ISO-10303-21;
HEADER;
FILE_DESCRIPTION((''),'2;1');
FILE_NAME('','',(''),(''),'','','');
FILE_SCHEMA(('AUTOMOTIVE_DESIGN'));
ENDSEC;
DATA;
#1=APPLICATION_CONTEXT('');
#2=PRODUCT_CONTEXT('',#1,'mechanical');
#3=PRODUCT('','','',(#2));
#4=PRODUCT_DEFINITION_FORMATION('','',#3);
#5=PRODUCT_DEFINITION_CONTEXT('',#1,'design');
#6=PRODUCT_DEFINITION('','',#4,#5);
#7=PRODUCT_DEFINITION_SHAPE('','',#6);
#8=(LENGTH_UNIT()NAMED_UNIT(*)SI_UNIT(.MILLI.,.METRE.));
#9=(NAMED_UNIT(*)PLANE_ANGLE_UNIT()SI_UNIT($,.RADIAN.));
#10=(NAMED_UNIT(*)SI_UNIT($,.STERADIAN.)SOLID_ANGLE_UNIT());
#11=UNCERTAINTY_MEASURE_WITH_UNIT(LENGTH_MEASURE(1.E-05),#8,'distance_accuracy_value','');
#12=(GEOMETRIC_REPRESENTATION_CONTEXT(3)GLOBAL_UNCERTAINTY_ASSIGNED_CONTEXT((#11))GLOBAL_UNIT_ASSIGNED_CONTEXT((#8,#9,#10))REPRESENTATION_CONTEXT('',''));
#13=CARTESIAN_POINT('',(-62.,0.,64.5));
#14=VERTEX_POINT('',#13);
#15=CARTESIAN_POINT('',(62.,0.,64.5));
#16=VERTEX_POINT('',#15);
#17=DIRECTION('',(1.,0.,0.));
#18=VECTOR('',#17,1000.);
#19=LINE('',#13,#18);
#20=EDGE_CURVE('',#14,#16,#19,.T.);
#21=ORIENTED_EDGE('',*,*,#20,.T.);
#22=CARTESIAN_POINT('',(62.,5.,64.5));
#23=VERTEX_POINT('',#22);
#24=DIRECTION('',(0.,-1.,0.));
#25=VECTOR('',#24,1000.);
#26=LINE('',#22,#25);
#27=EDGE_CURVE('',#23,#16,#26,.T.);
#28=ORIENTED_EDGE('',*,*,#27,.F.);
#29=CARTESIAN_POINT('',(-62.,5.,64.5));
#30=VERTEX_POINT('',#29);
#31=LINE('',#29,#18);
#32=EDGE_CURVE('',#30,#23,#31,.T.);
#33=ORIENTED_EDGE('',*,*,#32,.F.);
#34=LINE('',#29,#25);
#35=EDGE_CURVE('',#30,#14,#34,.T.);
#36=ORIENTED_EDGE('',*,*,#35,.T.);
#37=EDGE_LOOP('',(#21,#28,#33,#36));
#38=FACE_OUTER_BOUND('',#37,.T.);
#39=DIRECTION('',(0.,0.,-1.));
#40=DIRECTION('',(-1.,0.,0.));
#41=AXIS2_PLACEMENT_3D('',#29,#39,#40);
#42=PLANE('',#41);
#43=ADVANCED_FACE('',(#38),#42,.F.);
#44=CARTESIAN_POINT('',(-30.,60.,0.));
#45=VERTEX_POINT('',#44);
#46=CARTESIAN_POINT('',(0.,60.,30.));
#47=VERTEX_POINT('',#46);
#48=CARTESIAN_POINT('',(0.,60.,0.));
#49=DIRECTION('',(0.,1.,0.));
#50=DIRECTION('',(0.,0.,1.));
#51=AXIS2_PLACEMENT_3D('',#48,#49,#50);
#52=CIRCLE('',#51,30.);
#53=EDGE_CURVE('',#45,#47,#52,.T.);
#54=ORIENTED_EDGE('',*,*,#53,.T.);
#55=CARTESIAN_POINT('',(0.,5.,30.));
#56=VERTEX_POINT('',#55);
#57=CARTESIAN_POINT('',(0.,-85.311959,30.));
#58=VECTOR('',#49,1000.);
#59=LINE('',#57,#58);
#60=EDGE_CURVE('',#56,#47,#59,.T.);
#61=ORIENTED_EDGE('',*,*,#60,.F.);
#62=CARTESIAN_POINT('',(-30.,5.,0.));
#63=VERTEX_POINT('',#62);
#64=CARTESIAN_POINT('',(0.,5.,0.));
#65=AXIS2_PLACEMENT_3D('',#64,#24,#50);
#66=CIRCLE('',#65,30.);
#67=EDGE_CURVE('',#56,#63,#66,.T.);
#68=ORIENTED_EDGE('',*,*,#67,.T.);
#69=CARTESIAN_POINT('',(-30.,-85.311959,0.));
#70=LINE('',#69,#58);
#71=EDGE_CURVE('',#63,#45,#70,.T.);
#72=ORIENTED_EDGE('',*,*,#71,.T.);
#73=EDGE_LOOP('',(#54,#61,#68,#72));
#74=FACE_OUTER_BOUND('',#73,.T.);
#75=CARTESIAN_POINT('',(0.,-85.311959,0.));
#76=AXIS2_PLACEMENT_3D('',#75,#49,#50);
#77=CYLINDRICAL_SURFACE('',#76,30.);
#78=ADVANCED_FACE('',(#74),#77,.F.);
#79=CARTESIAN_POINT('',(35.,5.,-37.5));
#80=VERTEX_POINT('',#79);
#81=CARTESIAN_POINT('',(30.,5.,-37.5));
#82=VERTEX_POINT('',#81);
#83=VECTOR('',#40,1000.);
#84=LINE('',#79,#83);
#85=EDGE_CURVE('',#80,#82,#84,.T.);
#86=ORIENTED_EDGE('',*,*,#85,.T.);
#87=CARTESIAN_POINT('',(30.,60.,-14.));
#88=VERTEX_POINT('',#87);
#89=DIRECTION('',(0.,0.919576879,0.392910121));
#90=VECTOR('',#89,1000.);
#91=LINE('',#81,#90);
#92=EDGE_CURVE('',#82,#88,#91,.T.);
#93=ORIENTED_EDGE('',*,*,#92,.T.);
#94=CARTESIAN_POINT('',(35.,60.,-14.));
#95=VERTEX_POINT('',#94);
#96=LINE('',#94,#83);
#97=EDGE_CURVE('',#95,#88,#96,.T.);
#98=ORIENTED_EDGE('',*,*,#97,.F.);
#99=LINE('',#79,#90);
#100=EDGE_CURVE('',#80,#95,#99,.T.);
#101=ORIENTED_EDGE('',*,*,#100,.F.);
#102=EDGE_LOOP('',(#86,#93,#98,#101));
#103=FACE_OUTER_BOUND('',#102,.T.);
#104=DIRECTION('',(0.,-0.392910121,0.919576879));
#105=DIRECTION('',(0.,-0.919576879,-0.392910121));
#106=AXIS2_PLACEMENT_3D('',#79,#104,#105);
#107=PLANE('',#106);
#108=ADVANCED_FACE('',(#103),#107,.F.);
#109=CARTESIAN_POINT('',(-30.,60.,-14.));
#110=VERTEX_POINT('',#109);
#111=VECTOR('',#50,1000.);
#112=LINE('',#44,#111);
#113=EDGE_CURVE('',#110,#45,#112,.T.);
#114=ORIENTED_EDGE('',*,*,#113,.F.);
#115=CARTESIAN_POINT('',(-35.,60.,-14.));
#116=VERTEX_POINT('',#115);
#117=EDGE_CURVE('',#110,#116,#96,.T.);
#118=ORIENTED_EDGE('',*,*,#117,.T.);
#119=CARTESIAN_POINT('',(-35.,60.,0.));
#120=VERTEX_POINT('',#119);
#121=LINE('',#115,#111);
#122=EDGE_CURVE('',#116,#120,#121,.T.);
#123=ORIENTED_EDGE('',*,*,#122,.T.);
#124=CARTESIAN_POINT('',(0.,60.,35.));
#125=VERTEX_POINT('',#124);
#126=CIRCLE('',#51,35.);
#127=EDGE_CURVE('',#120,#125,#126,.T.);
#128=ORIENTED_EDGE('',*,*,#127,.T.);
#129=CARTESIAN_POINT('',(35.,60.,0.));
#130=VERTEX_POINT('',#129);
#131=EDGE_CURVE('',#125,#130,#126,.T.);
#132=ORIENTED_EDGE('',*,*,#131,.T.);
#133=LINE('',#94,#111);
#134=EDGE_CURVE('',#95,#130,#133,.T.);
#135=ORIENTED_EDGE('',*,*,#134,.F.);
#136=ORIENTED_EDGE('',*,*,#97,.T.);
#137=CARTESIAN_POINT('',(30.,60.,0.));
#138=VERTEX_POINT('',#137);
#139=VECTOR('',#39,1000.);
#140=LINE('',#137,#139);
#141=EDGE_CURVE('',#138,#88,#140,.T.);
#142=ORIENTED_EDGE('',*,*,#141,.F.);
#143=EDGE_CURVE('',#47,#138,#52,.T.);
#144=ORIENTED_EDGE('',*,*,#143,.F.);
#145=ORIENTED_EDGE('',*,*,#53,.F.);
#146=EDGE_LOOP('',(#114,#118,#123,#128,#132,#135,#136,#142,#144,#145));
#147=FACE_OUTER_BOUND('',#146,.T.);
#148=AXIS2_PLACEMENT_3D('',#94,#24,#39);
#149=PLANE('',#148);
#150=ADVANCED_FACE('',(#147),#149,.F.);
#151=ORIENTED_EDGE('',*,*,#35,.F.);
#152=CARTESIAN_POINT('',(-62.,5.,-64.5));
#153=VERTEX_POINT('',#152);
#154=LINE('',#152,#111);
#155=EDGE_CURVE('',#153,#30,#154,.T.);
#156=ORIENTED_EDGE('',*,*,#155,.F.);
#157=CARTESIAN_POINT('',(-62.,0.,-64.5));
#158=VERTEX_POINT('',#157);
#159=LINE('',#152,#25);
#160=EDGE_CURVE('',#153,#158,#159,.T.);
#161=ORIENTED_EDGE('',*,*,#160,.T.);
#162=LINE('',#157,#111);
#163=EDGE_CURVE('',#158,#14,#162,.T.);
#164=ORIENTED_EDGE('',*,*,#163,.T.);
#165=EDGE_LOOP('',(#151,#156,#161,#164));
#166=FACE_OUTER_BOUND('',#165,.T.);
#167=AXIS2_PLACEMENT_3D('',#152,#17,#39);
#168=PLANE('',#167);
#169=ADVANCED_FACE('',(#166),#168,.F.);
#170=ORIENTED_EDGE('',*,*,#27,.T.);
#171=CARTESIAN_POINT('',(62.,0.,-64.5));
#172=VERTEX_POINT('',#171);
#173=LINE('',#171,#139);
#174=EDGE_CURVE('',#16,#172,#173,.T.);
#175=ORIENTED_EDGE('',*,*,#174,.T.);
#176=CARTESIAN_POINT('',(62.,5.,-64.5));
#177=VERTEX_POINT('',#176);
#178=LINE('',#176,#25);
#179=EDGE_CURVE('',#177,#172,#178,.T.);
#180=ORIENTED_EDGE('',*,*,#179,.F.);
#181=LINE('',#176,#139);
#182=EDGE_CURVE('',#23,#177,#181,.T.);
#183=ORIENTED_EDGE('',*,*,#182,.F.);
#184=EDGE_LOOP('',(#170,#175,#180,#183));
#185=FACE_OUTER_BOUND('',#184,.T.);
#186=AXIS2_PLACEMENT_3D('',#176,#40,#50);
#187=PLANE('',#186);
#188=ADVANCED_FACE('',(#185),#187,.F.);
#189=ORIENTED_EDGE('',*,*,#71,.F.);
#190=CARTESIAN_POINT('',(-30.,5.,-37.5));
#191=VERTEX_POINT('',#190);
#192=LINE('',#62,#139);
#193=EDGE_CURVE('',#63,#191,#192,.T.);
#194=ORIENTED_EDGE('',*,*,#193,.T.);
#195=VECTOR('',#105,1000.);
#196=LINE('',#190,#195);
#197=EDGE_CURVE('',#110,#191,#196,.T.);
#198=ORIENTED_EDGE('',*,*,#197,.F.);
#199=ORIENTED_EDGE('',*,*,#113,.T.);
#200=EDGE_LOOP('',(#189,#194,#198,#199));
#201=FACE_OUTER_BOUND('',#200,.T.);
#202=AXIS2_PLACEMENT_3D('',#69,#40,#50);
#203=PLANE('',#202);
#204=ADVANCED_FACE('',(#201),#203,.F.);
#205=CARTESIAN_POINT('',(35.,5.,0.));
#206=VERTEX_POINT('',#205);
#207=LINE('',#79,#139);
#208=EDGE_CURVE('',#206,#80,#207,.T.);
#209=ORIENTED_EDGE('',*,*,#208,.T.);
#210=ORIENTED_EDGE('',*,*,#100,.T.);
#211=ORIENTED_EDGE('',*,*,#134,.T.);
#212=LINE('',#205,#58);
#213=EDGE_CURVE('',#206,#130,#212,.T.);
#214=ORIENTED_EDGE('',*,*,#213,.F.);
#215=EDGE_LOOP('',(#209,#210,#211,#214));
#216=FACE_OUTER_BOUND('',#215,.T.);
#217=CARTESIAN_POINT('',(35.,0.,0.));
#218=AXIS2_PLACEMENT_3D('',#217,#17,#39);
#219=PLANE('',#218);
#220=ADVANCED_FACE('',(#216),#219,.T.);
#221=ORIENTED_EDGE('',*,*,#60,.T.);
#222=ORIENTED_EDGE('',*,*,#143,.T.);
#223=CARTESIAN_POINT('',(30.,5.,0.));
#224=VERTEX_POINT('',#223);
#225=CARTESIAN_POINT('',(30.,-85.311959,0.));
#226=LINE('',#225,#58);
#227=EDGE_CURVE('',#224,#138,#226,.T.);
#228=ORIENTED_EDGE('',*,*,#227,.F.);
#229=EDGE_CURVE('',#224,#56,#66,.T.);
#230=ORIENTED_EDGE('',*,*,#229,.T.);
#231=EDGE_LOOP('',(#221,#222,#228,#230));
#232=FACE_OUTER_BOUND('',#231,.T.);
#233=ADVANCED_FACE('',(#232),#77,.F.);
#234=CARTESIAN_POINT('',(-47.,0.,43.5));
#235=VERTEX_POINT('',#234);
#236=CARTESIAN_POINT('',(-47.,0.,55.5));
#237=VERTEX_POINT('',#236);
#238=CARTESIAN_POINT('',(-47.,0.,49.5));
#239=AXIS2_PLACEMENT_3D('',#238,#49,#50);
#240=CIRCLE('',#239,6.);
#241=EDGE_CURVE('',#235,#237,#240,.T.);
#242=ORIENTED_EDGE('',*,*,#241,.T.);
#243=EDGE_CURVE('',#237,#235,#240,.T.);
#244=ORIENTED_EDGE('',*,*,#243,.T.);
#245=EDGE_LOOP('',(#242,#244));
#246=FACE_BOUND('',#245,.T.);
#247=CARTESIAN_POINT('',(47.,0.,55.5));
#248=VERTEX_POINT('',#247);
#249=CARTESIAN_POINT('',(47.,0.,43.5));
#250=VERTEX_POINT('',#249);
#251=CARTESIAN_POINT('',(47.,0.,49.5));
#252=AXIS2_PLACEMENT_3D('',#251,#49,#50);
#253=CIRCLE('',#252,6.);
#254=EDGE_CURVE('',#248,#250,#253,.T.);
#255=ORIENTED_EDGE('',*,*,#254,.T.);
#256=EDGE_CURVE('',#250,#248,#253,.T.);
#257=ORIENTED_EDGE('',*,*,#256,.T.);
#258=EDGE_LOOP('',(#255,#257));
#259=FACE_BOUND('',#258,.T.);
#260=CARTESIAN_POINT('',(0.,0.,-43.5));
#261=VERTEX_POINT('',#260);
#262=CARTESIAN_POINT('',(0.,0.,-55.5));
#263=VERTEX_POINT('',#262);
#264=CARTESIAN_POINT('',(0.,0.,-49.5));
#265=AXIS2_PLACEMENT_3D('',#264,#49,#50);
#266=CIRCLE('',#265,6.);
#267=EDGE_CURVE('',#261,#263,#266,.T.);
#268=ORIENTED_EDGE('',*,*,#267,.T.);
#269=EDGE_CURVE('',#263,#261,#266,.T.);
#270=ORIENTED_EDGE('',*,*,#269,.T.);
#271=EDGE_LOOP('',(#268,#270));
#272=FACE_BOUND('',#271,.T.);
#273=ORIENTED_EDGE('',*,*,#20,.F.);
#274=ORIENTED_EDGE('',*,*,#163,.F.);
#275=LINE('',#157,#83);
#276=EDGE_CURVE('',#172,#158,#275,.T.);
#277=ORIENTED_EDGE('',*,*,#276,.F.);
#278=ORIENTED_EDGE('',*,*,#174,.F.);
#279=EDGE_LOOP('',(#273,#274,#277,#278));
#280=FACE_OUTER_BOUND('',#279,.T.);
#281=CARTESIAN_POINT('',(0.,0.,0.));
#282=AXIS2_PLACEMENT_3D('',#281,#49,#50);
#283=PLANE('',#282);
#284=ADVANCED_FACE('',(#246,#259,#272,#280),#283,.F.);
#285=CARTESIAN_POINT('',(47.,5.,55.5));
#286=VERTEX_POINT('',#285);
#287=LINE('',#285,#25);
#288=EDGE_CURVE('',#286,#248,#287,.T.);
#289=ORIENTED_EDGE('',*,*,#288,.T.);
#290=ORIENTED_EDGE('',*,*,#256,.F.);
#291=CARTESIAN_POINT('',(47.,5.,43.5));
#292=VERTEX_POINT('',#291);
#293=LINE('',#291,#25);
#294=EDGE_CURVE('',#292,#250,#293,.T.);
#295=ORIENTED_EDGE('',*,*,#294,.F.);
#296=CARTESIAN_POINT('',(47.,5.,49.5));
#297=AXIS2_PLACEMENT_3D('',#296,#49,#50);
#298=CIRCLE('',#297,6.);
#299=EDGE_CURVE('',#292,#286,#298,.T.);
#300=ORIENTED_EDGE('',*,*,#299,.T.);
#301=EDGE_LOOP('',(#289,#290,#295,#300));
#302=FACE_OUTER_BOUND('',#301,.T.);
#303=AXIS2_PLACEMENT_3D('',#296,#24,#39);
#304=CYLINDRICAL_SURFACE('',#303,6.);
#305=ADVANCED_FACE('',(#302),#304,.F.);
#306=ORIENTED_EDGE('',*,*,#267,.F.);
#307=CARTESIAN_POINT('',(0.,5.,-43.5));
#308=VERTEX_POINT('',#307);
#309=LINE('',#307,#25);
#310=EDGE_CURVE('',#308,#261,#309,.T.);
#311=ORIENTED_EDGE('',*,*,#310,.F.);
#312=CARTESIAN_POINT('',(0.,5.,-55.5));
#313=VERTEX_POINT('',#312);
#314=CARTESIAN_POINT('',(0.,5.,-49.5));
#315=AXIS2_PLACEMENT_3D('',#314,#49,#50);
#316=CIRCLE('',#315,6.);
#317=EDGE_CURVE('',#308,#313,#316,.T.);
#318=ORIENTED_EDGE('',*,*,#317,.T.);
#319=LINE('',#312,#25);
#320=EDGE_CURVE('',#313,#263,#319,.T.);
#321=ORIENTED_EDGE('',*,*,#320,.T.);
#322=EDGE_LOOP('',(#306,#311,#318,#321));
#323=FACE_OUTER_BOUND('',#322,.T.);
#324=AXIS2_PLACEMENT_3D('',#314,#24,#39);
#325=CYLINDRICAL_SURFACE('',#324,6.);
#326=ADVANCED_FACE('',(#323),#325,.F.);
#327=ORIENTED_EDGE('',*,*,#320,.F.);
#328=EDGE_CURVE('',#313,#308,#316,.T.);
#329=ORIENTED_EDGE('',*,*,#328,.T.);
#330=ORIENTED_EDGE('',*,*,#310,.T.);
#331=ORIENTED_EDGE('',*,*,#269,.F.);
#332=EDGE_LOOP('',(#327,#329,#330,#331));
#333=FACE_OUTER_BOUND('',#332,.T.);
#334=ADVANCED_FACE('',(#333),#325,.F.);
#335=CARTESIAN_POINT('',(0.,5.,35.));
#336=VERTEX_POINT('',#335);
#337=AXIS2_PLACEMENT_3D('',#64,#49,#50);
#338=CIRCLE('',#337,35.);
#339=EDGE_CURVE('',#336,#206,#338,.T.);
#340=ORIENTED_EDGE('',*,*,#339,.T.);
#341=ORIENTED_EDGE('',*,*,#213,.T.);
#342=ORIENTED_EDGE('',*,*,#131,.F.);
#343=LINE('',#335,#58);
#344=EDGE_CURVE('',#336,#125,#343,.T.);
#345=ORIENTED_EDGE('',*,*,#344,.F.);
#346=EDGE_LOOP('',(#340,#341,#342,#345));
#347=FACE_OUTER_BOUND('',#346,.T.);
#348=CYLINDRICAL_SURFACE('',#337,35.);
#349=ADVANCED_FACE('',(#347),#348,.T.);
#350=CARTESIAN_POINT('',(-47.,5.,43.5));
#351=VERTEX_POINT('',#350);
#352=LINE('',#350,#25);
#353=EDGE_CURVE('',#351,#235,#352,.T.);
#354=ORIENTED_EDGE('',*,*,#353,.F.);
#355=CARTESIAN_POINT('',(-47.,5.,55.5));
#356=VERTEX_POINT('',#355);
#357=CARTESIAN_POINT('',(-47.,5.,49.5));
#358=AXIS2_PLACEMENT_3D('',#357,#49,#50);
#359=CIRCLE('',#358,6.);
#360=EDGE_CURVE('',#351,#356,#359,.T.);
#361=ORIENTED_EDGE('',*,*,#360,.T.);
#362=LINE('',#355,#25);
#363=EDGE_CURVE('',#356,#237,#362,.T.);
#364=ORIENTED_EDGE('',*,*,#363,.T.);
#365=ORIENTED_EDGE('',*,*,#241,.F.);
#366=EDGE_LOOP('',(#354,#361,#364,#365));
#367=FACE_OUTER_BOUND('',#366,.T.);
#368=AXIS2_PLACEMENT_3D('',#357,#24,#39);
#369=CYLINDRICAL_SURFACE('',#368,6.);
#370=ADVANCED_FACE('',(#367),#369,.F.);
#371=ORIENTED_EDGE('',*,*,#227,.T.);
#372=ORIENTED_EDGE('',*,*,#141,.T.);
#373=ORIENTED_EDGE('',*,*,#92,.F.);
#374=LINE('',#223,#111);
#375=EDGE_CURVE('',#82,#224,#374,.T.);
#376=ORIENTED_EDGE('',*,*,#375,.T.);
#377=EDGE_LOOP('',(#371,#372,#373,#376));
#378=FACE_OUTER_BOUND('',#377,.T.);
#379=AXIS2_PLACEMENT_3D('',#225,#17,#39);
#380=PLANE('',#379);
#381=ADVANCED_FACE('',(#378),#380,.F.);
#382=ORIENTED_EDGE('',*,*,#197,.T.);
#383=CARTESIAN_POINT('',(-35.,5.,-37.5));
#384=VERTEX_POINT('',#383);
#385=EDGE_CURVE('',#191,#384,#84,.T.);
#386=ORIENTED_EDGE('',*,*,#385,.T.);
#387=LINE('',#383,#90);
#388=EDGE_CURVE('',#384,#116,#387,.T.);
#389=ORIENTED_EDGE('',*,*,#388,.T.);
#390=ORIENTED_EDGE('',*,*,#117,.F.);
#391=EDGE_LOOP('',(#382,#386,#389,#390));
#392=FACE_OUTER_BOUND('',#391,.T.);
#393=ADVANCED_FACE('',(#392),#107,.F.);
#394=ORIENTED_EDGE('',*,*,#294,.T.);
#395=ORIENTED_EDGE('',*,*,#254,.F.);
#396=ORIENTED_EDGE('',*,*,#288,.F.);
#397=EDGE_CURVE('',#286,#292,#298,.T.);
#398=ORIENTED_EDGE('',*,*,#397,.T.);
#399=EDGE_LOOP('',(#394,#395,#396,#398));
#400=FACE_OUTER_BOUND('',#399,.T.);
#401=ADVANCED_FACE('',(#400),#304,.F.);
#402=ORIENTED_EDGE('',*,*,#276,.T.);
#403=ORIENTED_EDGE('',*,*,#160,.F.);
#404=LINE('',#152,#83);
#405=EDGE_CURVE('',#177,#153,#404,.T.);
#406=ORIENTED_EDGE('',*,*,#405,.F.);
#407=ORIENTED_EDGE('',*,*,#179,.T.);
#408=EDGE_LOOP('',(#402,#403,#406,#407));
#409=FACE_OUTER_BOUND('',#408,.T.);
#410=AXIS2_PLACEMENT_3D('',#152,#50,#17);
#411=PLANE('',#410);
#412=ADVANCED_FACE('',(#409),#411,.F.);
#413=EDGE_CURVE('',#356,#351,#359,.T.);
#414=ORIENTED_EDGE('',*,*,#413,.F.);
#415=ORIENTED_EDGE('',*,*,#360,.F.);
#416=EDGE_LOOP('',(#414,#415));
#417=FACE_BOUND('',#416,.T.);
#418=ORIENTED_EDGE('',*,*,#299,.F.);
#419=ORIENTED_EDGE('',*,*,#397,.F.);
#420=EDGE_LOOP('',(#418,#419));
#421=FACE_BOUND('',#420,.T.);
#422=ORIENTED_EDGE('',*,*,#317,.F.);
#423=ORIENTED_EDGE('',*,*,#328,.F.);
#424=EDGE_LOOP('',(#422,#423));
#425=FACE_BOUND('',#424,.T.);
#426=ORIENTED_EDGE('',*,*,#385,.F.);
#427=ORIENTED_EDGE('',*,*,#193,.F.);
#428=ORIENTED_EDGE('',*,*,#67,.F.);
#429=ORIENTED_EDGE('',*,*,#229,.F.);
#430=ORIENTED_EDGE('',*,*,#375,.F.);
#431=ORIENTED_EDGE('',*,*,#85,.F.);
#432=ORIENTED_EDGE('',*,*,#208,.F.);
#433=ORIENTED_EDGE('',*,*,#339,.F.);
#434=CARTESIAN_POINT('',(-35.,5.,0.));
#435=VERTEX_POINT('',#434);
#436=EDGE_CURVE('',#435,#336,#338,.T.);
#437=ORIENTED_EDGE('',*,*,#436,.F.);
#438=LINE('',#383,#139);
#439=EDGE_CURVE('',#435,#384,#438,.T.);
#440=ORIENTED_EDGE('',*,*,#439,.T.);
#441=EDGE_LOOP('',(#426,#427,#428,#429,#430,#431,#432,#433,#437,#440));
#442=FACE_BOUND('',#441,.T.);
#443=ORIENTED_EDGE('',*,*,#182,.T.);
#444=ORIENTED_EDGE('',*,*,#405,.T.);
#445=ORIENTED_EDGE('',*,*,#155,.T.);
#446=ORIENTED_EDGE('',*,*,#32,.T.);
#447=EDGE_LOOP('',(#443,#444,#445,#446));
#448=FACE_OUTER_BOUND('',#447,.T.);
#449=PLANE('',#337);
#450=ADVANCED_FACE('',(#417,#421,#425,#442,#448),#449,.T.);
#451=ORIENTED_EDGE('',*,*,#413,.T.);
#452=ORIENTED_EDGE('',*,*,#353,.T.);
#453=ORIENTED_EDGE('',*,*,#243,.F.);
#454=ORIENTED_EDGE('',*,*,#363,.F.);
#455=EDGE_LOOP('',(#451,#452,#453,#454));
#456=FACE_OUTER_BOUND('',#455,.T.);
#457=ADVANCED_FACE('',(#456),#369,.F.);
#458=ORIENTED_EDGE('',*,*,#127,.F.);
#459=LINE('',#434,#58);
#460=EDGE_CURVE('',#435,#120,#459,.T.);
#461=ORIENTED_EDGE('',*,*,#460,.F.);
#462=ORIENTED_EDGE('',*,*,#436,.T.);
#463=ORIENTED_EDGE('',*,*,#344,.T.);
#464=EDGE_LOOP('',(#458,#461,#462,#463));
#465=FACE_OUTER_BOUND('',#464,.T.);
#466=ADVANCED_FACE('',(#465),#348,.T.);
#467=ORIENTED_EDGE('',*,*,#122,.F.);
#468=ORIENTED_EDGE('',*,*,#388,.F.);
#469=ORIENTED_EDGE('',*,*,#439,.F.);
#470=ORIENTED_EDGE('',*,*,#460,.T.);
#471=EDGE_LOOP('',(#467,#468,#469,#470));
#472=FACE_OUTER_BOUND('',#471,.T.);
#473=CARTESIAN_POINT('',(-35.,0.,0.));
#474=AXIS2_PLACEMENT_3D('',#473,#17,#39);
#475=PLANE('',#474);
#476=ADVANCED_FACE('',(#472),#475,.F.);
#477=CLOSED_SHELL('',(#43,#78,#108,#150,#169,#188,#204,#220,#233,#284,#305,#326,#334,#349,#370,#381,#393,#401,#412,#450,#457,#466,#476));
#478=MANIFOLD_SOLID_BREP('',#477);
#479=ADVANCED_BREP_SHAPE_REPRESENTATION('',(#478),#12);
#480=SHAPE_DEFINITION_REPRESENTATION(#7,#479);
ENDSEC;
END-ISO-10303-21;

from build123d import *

# Parameters (mm, degrees)
BASE_PLATE_SKETCH_W         = 124
BASE_PLATE_SKETCH_H         = 129
BASE_PLATE_SKETCH_R         = 6
BASE_PLATE_DEPTH            = 5
UPRIGHT_SUPPORT_BLOCK_DEPTH = 35
CRADLE_CUT_SKETCH_W         = 60
CRADLE_CUT_SKETCH_H         = 23.5
CRADLE_CUT_DEPTH            = 55
GUSSET_TRIM_CUT_DEPTH       = 55


with BuildPart() as part:
    # Base Plate Sketch → Base Plate (new body)
    with BuildSketch(Plane(origin=(0, 0, 0), x_dir=(1, 0, 0), z_dir=(0, 1, 0))):
        Rectangle(BASE_PLATE_SKETCH_W, BASE_PLATE_SKETCH_H)
        with Locations(Location((0, 49.5, 0), (0, 0, 270))):
            Circle(BASE_PLATE_SKETCH_R, mode=Mode.SUBTRACT)
        with Locations(Location((47, -49.5, 0), (0, 0, 270))):
            Circle(BASE_PLATE_SKETCH_R, mode=Mode.SUBTRACT)
        with Locations(Location((-47, -49.5, 0), (0, 0, 270))):
            Circle(BASE_PLATE_SKETCH_R, mode=Mode.SUBTRACT)
    extrude(amount=BASE_PLATE_DEPTH)

    # Upright Support Profile Sketch → Upright Support Block (add, symmetric)
    with BuildSketch(Plane(origin=(0, 0, 0), x_dir=(0, 0, -1), z_dir=(1, 0, 0))):
        Polygon((37.5, 5), (14, 60), (-35, 60), (-35, 5), align=None)
    extrude(amount=UPRIGHT_SUPPORT_BLOCK_DEPTH, both=True)

    # Cradle Cut Sketch → Cradle Cut (cut)
    with BuildSketch(Plane(origin=(0, 60, 0), x_dir=(1, 0, 0), z_dir=(0, 1, 0))):
        with Locations((0, 25.75)):
            Rectangle(CRADLE_CUT_SKETCH_W, CRADLE_CUT_SKETCH_H)
        with BuildLine():
            Line((30, 14), (-30, 14))
            Line((-30, 14), (-30, 0))
            ThreePointArc((-30, 0), (0, -30), (30, 0))
            Line((30, 0), (30, 14))
        make_face()
    extrude(amount=-CRADLE_CUT_DEPTH, mode=Mode.SUBTRACT)

    # Gusset Trim Sketch → Gusset Trim Cut (cut)
    with BuildSketch(Plane(origin=(0, 60, 0), x_dir=(1, 0, 0), z_dir=(0, 1, 0))):
        with BuildLine():
            Line((-35, -35), (1.7e-07, -35))
            ThreePointArc((1.7e-07, -35), (-24.748737282, -24.748737402), (-35, 0))
            Line((-35, 0), (-35, -35))
        make_face()
        with BuildLine():
            Line((35, -35), (35, 0))
            ThreePointArc((35, 0), (24.748737402, -24.748737282), (1.7e-07, -35))
            Line((1.7e-07, -35), (35, -35))
        make_face()
    extrude(amount=-GUSSET_TRIM_CUT_DEPTH, mode=Mode.SUBTRACT)


solid = part.part
